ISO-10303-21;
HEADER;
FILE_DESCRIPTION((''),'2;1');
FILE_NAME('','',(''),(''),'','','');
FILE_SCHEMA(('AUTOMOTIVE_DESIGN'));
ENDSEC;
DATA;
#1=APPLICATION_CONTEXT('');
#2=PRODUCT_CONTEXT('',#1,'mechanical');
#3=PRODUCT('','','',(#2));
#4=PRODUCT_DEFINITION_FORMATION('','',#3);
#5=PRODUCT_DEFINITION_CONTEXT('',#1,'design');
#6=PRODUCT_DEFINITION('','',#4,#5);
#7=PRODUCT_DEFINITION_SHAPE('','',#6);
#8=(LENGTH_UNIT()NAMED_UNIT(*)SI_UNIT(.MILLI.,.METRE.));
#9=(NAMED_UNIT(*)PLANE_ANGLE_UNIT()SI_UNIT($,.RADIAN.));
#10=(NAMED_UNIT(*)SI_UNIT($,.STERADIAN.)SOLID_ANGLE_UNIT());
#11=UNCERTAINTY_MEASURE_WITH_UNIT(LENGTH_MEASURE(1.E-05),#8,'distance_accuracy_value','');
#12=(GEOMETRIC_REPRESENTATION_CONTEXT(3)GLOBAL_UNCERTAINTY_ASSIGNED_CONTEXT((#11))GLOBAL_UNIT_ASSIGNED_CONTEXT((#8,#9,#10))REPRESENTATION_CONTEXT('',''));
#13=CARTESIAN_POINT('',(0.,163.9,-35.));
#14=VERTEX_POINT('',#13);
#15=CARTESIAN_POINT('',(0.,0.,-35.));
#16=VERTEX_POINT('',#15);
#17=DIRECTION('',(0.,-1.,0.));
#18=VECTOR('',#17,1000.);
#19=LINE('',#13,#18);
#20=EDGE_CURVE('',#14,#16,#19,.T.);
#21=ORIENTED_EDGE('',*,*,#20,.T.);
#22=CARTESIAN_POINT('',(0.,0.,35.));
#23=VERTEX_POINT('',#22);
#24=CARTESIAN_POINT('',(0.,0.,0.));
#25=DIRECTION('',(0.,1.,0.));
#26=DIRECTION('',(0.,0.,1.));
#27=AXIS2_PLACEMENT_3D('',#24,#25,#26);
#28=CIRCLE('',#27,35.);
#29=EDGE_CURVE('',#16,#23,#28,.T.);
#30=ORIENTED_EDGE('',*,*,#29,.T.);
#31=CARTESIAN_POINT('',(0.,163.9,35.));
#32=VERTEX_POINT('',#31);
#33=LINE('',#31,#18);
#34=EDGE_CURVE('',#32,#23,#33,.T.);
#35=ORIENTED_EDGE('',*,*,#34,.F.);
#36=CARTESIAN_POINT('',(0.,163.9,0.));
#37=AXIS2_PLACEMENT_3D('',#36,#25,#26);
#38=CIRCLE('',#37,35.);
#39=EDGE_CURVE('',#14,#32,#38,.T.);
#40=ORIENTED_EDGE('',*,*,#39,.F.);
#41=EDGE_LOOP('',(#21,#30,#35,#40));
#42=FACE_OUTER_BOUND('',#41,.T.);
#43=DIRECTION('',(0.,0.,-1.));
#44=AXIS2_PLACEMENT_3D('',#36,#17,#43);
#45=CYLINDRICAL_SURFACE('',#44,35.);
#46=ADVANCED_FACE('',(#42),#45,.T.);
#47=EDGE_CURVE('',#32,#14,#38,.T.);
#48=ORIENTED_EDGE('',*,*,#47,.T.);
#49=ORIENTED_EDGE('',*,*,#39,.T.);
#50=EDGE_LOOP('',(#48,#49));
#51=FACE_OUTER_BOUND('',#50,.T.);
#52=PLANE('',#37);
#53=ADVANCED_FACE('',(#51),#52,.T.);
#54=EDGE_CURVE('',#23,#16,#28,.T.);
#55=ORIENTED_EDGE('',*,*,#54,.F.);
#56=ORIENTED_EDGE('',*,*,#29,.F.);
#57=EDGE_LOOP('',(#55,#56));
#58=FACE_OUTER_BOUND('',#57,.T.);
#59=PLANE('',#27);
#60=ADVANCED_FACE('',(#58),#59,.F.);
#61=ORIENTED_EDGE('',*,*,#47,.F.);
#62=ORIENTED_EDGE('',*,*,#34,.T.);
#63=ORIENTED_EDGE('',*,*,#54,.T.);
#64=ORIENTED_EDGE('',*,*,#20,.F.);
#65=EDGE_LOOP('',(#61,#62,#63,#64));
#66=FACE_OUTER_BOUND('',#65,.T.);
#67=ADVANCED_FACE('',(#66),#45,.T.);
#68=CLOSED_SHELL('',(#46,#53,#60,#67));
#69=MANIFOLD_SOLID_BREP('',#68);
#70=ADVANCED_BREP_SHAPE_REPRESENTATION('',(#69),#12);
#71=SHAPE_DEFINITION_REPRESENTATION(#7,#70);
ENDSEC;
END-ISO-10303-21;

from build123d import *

# Parameters (mm, degrees)
SKETCH1_R           = 35
BOSS_EXTRUDE1_DEPTH = 163.9


with BuildPart() as part:
    # Sketch1 → Boss-Extrude1 (new body)
    with BuildSketch(Plane(origin=(0, 0, 0), x_dir=(1, 0, 0), z_dir=(0, 1, 0))):
        with Locations(Location((0, 0, 0), (0, 0, 270))):
            Circle(SKETCH1_R)
    extrude(amount=BOSS_EXTRUDE1_DEPTH)


solid = part.part
